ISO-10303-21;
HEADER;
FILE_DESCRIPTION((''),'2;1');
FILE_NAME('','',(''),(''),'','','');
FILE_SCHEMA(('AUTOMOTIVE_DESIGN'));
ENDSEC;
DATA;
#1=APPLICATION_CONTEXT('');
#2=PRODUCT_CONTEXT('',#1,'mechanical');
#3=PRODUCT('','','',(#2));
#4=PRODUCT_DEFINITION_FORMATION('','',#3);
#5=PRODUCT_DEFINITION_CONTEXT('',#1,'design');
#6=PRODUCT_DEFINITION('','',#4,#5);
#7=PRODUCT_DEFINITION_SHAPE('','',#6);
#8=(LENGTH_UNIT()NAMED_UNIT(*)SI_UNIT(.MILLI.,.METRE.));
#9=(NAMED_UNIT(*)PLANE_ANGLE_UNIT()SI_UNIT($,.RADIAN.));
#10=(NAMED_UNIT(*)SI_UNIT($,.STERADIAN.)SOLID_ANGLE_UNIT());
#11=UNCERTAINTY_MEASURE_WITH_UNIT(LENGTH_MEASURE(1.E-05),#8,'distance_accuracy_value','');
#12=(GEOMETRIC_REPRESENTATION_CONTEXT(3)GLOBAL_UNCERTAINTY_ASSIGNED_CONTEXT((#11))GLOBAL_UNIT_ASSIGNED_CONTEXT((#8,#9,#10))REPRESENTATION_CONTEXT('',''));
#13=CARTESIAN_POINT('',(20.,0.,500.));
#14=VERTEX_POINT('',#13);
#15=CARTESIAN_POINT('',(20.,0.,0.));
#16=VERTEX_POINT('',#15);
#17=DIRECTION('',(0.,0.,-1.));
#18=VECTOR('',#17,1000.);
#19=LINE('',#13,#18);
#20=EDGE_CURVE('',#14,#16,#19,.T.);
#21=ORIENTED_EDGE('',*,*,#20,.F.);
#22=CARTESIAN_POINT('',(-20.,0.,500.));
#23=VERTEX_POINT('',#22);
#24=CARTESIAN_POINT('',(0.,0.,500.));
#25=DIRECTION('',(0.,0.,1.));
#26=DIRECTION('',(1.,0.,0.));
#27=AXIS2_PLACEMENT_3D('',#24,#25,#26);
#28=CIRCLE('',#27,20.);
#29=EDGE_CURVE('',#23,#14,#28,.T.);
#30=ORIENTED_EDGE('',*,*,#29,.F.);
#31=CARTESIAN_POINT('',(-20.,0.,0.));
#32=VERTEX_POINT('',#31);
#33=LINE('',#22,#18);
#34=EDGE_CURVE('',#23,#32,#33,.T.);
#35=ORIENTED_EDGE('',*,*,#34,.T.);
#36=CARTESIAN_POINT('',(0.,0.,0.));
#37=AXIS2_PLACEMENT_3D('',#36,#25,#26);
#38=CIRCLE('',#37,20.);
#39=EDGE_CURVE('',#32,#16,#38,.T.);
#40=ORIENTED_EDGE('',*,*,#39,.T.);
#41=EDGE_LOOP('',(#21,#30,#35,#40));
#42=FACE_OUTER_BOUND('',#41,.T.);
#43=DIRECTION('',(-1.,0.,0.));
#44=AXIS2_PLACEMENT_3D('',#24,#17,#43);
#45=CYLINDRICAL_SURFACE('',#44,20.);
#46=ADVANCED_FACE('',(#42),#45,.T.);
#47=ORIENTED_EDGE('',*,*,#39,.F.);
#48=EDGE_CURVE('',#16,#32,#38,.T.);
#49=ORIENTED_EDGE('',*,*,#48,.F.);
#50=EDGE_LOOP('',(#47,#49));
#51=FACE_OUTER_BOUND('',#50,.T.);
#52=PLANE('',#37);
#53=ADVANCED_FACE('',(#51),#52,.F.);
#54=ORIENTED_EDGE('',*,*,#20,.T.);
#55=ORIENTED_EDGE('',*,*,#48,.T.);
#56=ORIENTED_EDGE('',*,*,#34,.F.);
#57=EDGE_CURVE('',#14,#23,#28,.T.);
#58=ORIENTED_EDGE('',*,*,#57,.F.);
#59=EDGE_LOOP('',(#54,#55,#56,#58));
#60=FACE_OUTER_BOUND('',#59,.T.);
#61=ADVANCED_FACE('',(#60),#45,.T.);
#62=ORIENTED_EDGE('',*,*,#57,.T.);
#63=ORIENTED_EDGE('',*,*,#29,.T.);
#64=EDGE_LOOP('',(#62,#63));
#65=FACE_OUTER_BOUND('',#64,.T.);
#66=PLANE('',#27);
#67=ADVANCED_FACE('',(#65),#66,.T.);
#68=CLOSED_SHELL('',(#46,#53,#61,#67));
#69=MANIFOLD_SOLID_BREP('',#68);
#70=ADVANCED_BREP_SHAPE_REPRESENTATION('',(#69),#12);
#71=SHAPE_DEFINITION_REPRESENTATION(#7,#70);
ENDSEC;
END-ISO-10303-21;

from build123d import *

# Parameters (mm, degrees)
SKETCH1_R           = 20
BOSS_EXTRUDE1_DEPTH = 500


with BuildPart() as part:
    # Sketch1 → Boss-Extrude1 (new body)
    with BuildSketch(Plane.XY):
        Circle(SKETCH1_R)
    extrude(amount=BOSS_EXTRUDE1_DEPTH)


solid = part.part
